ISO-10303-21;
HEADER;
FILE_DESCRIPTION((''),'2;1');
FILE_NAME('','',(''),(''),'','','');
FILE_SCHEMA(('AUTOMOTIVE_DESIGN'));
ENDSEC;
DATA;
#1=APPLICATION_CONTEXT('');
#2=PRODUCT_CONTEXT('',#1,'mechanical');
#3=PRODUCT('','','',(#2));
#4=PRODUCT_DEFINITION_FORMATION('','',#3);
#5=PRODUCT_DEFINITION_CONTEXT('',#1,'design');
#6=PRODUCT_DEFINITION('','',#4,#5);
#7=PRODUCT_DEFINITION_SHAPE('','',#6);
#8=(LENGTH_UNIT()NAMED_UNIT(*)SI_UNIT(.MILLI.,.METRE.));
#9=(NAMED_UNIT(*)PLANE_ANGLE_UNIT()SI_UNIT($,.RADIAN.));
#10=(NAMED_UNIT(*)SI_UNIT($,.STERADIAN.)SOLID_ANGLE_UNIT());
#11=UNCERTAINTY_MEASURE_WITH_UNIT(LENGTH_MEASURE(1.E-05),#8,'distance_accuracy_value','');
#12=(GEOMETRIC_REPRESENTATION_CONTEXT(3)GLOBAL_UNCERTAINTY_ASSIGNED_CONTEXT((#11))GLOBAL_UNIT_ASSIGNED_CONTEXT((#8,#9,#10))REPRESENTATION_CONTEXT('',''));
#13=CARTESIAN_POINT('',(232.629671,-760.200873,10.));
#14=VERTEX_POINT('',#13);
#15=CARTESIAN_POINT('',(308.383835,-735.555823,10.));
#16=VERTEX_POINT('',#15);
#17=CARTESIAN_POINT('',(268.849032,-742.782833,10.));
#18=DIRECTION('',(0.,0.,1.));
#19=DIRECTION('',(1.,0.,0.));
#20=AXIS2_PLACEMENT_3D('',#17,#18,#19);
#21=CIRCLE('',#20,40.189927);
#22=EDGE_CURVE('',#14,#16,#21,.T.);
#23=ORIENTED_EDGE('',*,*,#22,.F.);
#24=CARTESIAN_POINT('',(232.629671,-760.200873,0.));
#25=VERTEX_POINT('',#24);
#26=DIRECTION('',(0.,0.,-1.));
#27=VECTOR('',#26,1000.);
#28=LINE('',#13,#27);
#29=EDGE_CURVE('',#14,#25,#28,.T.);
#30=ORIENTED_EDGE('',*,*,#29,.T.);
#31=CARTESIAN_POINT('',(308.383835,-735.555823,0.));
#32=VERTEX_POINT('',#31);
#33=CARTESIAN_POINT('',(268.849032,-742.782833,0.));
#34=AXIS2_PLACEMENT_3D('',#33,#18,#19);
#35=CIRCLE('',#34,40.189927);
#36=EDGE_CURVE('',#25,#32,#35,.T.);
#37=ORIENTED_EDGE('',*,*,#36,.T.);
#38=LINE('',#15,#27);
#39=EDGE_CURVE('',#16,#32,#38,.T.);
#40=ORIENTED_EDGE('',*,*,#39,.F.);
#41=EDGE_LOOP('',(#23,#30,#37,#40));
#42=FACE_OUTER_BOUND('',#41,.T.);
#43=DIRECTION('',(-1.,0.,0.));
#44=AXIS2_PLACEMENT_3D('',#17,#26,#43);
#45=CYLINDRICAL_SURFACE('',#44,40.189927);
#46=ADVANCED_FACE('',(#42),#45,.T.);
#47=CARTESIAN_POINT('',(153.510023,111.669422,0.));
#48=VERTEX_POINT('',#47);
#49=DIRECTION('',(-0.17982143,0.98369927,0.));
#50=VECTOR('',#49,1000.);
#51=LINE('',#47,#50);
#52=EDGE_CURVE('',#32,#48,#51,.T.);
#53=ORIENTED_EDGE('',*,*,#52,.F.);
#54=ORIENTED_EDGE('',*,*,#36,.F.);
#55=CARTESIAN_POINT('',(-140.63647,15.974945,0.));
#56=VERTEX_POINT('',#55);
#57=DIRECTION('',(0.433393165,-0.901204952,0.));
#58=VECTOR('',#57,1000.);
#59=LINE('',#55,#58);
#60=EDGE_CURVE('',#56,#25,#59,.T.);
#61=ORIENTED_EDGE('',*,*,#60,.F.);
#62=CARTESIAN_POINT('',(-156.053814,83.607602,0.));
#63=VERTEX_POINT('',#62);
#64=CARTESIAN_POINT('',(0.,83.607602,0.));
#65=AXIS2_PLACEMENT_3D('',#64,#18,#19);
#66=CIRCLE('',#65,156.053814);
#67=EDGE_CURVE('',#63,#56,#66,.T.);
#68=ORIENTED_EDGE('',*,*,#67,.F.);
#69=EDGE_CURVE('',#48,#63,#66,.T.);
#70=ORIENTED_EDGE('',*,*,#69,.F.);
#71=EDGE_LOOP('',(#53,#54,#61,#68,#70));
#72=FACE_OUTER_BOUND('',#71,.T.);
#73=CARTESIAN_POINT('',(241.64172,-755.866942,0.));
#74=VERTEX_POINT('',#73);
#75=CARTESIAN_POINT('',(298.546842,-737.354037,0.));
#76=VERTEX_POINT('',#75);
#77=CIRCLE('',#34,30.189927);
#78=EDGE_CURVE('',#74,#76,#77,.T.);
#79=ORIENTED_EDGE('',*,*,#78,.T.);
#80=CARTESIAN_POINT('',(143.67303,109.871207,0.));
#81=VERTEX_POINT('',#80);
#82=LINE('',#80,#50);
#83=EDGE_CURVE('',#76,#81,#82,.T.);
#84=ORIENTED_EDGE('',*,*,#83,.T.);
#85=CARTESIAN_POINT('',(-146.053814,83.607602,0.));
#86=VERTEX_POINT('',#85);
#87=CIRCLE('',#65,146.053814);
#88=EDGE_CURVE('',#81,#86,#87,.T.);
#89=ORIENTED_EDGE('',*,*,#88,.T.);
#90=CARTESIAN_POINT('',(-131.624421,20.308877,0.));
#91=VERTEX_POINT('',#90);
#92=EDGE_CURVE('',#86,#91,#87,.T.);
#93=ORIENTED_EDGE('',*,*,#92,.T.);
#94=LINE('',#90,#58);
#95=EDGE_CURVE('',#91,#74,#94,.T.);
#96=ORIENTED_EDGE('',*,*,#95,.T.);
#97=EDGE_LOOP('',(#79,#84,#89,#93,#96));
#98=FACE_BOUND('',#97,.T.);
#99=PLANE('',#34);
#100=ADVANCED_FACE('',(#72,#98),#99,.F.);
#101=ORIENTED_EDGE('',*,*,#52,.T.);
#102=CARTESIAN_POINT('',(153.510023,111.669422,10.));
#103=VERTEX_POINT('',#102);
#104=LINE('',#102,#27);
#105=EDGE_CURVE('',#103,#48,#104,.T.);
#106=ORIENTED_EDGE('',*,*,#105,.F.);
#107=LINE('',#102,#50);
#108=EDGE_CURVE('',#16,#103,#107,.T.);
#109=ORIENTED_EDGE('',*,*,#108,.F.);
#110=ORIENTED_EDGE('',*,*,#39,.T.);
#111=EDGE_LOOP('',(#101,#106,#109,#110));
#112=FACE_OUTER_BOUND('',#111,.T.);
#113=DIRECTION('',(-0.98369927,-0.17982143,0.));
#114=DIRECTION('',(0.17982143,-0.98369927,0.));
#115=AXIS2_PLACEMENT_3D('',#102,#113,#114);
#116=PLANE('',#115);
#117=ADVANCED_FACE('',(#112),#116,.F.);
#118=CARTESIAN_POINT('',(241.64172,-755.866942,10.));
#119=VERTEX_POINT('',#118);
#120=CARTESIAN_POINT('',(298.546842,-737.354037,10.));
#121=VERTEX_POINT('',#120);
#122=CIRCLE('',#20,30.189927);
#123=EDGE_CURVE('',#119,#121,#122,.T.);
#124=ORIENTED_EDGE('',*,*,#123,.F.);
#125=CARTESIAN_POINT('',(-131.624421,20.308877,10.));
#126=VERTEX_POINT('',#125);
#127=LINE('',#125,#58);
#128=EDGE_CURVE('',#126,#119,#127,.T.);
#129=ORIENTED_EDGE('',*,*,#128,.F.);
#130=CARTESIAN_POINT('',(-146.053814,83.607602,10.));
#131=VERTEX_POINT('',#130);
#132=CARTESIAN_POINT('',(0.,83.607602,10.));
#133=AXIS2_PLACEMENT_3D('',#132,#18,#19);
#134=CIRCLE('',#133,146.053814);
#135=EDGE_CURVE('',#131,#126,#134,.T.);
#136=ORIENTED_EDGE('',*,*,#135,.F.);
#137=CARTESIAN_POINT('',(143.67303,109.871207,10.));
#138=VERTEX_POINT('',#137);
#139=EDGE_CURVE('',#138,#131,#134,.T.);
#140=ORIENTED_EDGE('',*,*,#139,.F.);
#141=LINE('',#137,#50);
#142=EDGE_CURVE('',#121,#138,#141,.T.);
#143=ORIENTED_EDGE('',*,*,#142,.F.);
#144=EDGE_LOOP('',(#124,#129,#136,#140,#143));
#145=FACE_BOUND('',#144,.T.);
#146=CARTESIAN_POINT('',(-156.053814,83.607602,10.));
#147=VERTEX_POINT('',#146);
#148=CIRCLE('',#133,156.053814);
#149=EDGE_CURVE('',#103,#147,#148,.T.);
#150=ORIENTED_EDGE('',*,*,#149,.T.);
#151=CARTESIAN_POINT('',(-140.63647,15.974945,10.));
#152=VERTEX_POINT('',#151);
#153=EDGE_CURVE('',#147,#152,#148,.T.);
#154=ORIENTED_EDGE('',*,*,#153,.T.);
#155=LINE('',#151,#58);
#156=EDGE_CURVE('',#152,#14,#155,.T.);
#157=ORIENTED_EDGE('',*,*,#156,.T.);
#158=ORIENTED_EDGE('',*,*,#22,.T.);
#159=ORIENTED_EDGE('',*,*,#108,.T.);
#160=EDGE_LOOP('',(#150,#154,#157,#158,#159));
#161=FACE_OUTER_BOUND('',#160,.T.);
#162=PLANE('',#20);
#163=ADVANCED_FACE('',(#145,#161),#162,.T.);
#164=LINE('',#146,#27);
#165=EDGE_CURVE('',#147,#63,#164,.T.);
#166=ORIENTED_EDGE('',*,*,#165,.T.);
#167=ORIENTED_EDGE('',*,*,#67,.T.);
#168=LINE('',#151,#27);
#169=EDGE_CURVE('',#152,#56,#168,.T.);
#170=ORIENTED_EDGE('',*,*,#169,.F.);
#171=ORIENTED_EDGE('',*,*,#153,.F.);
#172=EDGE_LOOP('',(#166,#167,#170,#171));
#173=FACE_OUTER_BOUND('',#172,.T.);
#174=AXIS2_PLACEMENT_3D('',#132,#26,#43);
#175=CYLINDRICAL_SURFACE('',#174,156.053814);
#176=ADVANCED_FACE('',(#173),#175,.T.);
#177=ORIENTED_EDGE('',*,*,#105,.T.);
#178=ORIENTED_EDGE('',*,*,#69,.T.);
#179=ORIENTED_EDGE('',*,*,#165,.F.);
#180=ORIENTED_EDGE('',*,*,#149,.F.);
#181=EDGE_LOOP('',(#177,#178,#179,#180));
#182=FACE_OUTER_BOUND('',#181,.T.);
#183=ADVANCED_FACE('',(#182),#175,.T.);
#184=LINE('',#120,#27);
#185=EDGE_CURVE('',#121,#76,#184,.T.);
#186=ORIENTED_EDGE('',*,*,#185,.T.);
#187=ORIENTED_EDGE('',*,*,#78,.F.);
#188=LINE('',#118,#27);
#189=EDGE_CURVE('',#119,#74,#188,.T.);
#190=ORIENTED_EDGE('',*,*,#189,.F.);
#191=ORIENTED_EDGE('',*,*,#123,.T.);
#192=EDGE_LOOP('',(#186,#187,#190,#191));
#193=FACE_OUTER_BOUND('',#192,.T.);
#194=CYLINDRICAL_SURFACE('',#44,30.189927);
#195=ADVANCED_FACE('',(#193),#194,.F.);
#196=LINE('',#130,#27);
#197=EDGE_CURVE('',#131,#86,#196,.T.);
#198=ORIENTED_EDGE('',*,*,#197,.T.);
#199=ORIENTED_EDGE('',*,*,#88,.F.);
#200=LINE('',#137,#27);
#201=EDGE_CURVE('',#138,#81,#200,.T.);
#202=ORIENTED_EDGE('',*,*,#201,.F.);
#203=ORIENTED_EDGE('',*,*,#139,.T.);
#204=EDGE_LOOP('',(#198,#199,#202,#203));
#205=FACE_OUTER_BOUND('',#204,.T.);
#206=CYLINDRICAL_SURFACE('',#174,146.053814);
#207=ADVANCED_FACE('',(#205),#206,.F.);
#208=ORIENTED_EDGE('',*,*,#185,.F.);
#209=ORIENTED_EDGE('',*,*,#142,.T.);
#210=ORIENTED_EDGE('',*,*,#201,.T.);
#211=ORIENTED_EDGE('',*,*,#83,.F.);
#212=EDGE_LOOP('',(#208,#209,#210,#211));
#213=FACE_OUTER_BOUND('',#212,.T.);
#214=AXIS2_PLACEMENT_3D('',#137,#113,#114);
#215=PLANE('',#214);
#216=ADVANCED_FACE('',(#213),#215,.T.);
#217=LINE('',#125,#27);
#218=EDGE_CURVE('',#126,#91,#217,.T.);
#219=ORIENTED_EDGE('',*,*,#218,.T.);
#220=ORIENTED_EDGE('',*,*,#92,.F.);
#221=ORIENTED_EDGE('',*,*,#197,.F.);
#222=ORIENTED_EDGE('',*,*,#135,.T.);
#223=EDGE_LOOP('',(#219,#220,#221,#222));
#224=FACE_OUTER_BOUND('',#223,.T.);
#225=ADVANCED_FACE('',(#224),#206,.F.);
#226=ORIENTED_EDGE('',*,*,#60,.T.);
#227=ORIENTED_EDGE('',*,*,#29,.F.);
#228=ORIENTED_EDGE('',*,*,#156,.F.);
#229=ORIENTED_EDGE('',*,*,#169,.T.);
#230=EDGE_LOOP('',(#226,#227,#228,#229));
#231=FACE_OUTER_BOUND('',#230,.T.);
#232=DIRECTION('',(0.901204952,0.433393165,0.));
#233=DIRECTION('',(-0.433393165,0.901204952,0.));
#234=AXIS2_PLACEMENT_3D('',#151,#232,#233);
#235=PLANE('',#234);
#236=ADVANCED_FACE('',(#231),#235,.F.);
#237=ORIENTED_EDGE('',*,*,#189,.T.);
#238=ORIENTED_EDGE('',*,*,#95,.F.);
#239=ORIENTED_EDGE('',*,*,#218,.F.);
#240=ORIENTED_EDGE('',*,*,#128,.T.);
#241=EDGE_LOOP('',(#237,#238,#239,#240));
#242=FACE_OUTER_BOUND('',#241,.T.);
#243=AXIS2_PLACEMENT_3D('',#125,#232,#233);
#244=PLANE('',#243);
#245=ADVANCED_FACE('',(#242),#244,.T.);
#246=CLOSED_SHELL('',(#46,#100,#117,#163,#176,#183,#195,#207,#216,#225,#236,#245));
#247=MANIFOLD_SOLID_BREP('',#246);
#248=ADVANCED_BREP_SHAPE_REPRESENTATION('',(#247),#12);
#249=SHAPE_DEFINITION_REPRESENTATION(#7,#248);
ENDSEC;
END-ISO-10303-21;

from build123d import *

# Parameters (mm, degrees)
THIN_WALL_EXTRUDE1_DEPTH = 10


with BuildPart() as part:
    # Sketch1 → Thin-wall extrude1 (new body)
    with BuildSketch(Plane.XY):
        with BuildLine():
            Line((153.510023011, 111.669421793), (308.383834576, -735.55582317))
            ThreePointArc((308.383834576, -735.55582317), (281.282561977, -781.001122311), (232.629670707, -760.200873238))
            Line((232.629670707, -760.200873238), (-140.636470033, 15.974945367))
            ThreePointArc((-140.636470033, 15.974945367), (-48.278259042, 232.005723732), (153.510023011, 111.669421793))
        make_face()
        with BuildLine():
            Line((143.673030314, 109.87120749), (298.546841879, -737.354037473))
            ThreePointArc((298.546841879, -737.354037473), (278.18886899, -771.491702575), (241.641720223, -755.866941592))
            Line((241.641720223, -755.866941592), (-131.624420517, 20.308877014))
            ThreePointArc((-131.624420517, 20.308877014), (-45.184566055, 222.496303997), (143.673030314, 109.87120749))
        make_face(mode=Mode.SUBTRACT)
    extrude(amount=THIN_WALL_EXTRUDE1_DEPTH)


solid = part.part
